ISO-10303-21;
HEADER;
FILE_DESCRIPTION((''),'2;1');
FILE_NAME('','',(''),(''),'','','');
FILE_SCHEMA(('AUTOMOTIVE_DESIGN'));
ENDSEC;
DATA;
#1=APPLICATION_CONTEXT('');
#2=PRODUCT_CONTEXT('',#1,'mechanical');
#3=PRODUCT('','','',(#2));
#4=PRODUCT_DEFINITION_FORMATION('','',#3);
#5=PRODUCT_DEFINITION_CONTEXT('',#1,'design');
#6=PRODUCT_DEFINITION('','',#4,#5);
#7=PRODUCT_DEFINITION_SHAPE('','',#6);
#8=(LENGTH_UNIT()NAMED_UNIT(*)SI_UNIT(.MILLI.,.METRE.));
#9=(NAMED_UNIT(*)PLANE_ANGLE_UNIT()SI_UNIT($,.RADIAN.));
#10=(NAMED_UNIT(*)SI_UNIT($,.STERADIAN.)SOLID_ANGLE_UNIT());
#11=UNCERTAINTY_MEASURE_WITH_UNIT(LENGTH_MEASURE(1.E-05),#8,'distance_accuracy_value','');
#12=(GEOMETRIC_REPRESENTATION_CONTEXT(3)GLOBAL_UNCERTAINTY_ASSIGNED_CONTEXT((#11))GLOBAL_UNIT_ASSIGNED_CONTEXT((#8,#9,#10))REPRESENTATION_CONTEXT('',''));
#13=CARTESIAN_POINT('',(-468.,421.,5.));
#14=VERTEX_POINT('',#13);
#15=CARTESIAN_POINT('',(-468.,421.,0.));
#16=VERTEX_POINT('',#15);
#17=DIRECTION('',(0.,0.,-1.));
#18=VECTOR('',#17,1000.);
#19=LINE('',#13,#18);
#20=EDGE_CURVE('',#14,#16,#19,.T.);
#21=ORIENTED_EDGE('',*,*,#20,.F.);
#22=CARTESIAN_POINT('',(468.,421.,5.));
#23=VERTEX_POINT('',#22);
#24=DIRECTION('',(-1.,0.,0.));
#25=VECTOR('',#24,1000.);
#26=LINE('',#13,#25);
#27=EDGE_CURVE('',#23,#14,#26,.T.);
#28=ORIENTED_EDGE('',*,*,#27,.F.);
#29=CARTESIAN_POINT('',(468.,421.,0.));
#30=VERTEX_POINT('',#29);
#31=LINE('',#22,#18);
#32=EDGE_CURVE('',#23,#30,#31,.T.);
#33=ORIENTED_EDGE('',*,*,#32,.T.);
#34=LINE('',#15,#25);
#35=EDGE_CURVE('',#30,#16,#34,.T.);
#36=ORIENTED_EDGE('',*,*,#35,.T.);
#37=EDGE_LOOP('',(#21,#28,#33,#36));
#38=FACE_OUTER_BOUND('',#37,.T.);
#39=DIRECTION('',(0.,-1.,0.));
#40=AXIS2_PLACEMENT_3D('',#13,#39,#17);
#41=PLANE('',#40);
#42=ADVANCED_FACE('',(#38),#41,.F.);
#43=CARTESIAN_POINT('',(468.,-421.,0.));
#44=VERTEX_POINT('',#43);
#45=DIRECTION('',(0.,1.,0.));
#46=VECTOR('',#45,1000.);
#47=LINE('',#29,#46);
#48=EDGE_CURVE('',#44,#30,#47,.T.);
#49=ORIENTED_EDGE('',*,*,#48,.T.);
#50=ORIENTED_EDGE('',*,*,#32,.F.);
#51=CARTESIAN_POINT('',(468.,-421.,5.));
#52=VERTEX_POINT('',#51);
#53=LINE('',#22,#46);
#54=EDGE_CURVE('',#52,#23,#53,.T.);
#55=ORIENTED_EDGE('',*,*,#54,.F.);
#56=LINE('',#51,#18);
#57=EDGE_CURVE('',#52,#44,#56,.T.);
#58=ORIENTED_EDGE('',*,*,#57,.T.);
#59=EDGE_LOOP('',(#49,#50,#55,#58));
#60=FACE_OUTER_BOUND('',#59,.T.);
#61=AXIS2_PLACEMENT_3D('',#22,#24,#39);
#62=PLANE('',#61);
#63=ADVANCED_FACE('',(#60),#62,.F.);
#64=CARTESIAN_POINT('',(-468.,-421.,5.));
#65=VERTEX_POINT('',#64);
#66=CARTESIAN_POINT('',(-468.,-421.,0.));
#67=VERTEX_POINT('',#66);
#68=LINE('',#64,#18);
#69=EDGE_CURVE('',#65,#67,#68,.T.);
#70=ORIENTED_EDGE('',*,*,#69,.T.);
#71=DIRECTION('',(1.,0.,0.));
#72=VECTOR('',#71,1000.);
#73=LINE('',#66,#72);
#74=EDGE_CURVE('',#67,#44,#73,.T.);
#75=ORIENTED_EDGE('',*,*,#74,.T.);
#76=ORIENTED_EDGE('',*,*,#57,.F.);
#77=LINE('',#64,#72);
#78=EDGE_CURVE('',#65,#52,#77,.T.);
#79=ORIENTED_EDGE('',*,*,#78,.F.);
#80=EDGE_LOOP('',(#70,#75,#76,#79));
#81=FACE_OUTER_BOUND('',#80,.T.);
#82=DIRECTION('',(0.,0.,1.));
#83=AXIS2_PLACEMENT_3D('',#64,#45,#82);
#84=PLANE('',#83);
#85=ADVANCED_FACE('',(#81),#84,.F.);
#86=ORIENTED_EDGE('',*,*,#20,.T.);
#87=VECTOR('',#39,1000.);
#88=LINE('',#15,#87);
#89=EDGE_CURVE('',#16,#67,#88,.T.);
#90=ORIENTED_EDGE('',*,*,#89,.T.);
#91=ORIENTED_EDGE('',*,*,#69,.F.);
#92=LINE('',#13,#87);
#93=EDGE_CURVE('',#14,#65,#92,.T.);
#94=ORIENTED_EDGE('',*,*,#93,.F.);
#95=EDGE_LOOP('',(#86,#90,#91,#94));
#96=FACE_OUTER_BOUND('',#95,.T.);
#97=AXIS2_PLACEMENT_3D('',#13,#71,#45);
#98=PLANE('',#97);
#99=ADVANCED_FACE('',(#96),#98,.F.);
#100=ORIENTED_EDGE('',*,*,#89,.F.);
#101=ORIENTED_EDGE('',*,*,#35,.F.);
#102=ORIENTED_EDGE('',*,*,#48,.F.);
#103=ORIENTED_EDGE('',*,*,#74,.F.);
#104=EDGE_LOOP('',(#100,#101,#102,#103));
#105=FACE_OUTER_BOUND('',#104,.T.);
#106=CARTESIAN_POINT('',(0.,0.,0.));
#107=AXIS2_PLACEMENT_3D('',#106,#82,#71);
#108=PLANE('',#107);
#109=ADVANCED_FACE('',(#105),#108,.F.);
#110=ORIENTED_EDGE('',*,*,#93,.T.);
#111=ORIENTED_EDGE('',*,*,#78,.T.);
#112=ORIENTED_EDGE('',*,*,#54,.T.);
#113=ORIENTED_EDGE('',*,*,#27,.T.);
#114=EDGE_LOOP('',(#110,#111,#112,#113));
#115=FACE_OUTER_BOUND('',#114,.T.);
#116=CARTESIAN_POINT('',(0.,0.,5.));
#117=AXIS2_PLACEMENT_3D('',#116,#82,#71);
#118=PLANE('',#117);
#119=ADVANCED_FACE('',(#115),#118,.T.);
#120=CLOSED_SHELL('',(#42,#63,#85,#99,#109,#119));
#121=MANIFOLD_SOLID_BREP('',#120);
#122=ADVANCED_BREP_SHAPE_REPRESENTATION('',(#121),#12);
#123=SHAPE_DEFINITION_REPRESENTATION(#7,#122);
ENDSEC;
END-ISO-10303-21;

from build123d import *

# Parameters (mm, degrees)
SKETCH_1_W      = 936
SKETCH_1_H      = 842
EXTRUDE_1_DEPTH = 5


with BuildPart() as part:
    # 草图1 → 凸台-拉伸1 (new body)
    with BuildSketch(Plane.XY):
        Rectangle(SKETCH_1_W, SKETCH_1_H)
    extrude(amount=EXTRUDE_1_DEPTH)


solid = part.part
